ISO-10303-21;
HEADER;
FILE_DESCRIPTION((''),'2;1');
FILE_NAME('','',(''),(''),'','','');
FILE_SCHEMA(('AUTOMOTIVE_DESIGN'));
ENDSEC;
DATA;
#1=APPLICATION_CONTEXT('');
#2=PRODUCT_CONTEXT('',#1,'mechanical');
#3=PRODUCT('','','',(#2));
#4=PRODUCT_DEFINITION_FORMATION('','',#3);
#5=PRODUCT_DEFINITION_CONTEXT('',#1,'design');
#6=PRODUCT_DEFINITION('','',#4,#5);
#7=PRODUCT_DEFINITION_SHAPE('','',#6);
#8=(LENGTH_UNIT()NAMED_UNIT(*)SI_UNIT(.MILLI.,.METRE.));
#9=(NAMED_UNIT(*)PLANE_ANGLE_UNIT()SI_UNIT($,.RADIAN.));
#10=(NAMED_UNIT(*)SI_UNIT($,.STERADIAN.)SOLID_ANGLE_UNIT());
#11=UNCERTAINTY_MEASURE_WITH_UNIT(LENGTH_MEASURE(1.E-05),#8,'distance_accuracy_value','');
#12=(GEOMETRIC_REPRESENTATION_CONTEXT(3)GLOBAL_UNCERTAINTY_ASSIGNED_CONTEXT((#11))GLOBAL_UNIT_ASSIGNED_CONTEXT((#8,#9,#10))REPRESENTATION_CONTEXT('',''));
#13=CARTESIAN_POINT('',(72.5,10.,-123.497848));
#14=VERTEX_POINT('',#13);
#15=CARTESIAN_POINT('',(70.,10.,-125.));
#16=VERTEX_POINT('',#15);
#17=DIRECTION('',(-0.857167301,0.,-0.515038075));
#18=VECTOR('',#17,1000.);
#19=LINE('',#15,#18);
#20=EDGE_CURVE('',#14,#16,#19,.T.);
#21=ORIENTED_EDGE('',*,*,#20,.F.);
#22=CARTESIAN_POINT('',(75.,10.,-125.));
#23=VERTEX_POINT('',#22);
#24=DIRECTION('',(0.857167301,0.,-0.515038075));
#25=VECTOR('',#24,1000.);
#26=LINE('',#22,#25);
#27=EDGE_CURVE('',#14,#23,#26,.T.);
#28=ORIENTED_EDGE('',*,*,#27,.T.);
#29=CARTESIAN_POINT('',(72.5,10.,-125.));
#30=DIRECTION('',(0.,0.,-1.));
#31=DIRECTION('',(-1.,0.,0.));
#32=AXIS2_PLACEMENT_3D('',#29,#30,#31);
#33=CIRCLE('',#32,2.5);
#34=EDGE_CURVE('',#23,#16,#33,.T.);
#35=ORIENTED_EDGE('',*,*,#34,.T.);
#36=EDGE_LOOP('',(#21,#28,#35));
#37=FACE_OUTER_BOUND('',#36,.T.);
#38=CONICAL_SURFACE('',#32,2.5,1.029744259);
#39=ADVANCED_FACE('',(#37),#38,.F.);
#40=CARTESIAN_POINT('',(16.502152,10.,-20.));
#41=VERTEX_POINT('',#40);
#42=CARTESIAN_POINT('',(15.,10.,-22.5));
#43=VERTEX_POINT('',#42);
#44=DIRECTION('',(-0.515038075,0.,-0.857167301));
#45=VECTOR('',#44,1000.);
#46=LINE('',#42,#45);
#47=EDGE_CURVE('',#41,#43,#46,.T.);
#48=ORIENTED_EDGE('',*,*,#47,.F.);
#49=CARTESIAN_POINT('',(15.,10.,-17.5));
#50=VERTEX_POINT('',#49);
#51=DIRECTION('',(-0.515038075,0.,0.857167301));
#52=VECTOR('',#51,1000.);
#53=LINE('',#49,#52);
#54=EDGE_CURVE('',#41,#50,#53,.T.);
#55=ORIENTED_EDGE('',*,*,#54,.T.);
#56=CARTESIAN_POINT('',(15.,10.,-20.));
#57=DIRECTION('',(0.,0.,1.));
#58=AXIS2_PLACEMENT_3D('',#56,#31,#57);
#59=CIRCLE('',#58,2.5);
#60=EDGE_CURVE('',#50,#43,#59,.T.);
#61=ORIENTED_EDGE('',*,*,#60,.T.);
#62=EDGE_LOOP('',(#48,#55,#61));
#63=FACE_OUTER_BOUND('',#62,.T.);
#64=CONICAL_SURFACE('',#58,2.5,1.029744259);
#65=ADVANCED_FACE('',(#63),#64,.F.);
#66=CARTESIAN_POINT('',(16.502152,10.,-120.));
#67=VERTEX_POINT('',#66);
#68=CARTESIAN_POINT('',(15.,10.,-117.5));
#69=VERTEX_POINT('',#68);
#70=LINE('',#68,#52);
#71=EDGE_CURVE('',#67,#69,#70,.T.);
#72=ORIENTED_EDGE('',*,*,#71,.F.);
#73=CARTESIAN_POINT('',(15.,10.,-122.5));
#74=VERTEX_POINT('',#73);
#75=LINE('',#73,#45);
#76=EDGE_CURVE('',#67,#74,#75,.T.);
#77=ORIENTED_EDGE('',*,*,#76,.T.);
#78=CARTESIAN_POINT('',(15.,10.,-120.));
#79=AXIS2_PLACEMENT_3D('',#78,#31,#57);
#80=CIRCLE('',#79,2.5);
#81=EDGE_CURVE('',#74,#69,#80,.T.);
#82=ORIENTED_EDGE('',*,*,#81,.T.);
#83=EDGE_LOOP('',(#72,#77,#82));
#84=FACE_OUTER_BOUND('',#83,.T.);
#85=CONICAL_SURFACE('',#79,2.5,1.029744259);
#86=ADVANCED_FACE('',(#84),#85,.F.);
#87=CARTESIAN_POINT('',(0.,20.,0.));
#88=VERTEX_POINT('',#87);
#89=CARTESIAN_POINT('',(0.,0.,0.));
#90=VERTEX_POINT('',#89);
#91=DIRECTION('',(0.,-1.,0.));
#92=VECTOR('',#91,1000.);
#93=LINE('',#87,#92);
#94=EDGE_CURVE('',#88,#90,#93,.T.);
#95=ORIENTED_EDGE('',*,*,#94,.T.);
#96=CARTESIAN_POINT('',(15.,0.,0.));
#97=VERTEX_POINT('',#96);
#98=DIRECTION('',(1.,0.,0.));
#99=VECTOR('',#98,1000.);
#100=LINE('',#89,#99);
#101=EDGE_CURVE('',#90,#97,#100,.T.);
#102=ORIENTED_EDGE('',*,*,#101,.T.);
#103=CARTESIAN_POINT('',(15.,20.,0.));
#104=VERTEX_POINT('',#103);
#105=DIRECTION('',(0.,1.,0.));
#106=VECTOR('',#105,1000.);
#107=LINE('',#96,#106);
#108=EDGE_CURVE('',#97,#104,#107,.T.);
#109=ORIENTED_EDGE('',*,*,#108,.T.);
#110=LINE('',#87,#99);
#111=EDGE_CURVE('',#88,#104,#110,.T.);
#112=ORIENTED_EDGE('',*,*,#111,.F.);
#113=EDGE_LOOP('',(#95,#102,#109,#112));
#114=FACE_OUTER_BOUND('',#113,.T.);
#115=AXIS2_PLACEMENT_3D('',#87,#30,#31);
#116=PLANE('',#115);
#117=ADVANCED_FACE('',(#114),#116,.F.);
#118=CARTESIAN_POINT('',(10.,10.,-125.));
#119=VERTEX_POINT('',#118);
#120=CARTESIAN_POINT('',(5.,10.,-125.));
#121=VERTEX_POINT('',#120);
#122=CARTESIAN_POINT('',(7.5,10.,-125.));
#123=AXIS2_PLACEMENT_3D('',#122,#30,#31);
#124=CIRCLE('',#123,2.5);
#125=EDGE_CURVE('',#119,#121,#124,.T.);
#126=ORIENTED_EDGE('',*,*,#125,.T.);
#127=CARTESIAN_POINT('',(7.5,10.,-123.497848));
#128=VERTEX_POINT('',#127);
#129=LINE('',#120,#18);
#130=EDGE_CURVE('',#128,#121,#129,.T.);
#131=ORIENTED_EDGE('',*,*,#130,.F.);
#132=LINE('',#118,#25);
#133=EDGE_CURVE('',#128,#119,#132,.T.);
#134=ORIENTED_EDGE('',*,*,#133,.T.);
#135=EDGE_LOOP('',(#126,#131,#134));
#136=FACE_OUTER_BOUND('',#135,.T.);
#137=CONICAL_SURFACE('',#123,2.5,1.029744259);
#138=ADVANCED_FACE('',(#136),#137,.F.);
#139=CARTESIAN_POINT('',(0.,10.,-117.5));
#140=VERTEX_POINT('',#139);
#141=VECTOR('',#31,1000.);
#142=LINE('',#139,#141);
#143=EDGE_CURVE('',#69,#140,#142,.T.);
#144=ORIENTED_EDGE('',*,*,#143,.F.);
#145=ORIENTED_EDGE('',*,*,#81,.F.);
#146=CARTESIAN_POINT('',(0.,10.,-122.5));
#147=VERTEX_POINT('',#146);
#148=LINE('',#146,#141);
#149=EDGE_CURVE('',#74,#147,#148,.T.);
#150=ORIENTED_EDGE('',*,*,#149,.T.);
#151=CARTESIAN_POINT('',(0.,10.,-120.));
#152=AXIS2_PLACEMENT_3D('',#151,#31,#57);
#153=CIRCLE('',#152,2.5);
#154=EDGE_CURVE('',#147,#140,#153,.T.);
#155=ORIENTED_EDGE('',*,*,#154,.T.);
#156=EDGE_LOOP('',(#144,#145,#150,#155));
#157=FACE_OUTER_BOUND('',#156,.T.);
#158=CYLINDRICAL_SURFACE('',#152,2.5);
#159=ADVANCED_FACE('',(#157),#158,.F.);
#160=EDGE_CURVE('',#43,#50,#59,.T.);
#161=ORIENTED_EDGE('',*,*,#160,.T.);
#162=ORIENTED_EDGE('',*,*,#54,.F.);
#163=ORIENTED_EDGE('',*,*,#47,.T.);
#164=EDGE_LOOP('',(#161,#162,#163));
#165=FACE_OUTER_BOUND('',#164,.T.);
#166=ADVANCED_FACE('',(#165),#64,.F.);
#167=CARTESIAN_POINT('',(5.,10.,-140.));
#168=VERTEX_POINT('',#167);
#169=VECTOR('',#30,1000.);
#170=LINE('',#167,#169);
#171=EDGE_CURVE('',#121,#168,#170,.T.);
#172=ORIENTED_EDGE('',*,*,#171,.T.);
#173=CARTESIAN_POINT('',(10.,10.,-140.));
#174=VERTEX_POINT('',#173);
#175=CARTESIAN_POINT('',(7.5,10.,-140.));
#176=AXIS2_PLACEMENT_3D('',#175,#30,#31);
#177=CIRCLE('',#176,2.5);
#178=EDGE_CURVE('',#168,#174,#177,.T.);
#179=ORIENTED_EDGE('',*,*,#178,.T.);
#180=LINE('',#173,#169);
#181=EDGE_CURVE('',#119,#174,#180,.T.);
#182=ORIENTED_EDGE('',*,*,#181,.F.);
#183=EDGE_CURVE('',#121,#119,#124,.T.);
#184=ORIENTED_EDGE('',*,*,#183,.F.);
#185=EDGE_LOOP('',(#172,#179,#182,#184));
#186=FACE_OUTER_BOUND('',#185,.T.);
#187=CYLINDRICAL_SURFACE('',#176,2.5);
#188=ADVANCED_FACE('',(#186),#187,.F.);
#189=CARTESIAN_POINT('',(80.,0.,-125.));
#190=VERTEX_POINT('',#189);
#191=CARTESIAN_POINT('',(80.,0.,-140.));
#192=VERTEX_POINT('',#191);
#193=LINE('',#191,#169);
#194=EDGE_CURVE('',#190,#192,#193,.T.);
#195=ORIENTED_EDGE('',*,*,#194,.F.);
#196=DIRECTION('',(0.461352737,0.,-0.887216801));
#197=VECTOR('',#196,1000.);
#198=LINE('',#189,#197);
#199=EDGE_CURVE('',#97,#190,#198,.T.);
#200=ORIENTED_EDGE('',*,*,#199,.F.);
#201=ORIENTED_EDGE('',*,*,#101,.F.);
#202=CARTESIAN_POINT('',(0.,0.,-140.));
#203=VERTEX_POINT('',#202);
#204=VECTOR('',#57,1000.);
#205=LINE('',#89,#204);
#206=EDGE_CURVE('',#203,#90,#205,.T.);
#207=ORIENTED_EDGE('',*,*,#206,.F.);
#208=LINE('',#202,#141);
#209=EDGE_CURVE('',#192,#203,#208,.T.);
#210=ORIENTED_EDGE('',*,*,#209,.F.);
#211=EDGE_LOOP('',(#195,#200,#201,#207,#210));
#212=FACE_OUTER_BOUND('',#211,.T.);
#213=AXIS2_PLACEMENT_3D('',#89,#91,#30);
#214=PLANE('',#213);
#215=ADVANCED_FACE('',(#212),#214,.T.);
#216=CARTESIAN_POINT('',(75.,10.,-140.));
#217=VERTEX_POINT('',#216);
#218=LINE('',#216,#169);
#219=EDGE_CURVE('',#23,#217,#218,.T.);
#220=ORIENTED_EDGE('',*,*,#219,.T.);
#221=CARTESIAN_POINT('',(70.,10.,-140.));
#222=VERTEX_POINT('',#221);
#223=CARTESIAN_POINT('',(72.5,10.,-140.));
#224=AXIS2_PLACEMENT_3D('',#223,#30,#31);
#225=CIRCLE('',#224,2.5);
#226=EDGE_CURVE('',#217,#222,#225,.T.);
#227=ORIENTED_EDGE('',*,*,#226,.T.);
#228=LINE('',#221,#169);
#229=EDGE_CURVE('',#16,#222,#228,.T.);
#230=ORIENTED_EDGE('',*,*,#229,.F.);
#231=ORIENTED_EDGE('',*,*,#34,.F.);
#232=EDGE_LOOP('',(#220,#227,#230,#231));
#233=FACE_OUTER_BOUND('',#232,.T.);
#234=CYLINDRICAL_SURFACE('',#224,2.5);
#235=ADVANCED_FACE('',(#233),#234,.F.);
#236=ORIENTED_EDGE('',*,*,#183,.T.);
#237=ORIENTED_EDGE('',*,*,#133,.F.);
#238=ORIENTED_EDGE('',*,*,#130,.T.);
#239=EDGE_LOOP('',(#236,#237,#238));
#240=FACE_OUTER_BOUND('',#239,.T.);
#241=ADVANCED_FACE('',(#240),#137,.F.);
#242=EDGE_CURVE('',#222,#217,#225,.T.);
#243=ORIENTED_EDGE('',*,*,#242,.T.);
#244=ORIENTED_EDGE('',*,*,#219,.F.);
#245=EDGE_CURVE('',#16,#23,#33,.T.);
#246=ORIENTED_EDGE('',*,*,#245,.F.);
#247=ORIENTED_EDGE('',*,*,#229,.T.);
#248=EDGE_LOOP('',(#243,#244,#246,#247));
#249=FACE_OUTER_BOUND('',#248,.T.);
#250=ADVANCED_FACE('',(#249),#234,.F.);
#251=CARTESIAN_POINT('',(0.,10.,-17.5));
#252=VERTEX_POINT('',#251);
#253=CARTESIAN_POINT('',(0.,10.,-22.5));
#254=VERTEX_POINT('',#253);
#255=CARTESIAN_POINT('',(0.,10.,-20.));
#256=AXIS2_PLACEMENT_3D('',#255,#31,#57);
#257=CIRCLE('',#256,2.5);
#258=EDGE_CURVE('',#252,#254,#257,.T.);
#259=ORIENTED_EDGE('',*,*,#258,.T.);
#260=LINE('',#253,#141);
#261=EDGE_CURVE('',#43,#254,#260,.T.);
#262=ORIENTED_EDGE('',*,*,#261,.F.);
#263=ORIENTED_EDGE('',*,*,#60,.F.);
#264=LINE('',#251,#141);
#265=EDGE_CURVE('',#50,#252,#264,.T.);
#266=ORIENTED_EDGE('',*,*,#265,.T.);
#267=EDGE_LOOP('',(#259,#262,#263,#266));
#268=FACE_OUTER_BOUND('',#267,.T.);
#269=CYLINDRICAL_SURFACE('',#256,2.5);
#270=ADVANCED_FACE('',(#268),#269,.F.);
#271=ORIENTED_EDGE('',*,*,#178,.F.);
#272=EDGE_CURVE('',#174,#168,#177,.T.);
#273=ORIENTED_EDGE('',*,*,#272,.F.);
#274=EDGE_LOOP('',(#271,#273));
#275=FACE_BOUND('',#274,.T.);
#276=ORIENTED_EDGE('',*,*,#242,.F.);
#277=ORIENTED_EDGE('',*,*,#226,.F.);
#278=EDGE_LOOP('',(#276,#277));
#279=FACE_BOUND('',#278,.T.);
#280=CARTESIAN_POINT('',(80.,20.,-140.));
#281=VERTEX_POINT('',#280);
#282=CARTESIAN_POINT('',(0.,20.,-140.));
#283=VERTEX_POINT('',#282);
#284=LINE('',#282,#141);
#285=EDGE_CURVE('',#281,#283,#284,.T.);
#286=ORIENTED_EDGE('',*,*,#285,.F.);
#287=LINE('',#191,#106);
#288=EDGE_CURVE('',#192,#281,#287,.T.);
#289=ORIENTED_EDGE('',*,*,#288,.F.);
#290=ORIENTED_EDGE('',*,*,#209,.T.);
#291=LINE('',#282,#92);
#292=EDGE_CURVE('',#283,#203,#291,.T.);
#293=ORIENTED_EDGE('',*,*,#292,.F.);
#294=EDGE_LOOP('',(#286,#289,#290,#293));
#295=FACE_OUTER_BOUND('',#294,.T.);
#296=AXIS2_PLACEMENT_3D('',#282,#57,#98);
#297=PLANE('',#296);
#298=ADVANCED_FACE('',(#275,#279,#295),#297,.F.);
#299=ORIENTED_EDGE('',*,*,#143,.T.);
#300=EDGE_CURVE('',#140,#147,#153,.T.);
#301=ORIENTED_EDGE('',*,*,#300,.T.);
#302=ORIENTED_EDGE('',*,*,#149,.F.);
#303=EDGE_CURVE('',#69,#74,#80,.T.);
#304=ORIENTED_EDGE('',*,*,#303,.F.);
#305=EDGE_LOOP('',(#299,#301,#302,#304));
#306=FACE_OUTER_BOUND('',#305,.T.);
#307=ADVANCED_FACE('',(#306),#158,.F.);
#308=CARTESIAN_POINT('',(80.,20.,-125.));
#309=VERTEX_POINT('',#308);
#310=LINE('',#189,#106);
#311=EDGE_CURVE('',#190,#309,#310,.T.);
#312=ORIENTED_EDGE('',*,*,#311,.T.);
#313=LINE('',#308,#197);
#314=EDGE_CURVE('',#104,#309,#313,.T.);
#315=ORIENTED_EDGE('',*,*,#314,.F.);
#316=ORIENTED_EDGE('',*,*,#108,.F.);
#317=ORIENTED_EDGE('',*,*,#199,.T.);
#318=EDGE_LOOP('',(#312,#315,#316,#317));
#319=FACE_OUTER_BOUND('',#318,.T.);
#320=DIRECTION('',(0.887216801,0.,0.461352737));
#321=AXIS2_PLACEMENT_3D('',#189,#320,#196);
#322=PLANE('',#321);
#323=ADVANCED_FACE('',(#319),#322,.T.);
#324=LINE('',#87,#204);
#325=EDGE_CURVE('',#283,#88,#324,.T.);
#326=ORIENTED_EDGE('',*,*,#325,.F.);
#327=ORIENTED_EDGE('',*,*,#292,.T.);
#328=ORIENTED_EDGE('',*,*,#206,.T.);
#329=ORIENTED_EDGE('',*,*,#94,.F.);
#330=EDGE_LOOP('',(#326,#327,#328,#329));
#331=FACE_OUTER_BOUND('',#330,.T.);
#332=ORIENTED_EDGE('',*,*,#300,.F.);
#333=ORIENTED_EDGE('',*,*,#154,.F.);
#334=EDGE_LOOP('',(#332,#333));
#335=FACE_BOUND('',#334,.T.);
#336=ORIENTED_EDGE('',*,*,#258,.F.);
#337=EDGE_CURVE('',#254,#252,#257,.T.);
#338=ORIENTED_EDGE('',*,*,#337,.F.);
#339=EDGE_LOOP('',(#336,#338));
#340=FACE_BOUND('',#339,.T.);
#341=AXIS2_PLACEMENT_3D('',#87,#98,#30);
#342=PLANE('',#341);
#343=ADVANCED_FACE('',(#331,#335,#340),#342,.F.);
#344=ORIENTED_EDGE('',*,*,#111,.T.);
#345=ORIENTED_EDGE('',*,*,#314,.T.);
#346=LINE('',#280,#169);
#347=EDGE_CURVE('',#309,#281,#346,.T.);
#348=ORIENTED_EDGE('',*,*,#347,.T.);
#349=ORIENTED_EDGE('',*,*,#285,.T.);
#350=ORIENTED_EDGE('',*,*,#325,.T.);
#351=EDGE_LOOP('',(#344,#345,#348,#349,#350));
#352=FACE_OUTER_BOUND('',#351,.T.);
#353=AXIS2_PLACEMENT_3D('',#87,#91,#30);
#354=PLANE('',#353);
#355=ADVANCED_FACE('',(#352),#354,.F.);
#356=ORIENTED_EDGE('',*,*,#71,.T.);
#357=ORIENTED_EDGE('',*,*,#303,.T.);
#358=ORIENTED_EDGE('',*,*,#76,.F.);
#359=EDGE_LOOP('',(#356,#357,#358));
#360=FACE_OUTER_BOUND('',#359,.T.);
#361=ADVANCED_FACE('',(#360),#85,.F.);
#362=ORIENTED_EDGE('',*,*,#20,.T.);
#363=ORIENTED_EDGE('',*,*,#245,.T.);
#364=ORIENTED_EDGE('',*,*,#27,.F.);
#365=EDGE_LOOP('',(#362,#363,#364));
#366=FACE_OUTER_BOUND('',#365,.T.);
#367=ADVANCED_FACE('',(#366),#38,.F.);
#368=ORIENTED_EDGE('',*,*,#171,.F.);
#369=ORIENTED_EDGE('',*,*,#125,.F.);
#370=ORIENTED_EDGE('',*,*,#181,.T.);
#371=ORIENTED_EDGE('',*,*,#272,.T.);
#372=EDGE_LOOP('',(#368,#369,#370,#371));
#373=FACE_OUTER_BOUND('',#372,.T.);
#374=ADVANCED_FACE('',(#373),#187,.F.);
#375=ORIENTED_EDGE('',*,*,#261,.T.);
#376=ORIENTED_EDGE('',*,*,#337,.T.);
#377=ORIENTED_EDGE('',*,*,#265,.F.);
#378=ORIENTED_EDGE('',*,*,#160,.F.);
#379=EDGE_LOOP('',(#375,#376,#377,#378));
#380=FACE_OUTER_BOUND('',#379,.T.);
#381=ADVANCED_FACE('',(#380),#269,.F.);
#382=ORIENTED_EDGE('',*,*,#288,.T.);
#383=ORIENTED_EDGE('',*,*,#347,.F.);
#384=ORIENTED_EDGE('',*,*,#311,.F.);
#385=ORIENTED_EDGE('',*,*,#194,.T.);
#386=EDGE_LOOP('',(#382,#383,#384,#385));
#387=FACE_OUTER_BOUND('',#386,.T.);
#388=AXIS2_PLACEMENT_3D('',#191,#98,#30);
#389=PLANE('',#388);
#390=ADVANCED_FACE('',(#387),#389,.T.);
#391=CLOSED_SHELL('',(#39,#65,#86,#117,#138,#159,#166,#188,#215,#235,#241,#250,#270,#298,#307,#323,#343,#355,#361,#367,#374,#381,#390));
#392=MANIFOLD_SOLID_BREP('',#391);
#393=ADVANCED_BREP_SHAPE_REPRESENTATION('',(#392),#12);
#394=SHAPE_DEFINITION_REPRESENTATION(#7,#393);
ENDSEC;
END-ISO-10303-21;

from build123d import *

# Parameters (mm, degrees)
SKETCH_1_W             = 200
SKETCH_1_H             = 140
EXTRUDE_1_DEPTH        = 20
SKETCH_3_OUTSIDE_W     = 250.99
SKETCH_3_OUTSIDE_H     = 190.99
CUT_EXTRUDE_1_DEPTH    = 245.948974278
HOLE_WIZARD_M6_1_D     = 5
HOLE_WIZARD_M6_1_DEPTH = 15
HOLE_WIZARD_M6_1_TIP   = 1.502151548
HOLE_WIZARD_M6_2_D     = 5
HOLE_WIZARD_M6_2_DEPTH = 15
HOLE_WIZARD_M6_2_TIP   = 1.502151548


with BuildPart() as part:
    # 草图1 → 凸台-拉伸1 (new body)
    with BuildSketch(Plane(origin=(0, 0, 0), x_dir=(1, 0, 0), z_dir=(0, 1, 0))):
        with Locations((100, 70)):
            Rectangle(SKETCH_1_W, SKETCH_1_H)
    extrude(amount=EXTRUDE_1_DEPTH)

    # 草图3 outside → 切除-拉伸1 (cut, through all)
    with BuildSketch(Plane(origin=(0, 20, 0), x_dir=(1, 0, 0), z_dir=(0, 1, 0))):
        with Locations((100, 70)):
            Rectangle(SKETCH_3_OUTSIDE_W, SKETCH_3_OUTSIDE_H)
        Polygon((0, 140), (80, 140), (80, 125), (15, 0), (0, 0), align=None, mode=Mode.SUBTRACT)
    extrude(amount=-CUT_EXTRUDE_1_DEPTH, mode=Mode.SUBTRACT)

    # M6 螺纹孔1
    with Locations(Plane.ZY):
        with Locations((-120, 10), (-20, 10)):
            Hole(HOLE_WIZARD_M6_1_D / 2, depth=HOLE_WIZARD_M6_1_DEPTH)
            with Locations((0, 0, -(HOLE_WIZARD_M6_1_DEPTH + HOLE_WIZARD_M6_1_TIP / 2))):  # 118° drill point
                Cone(0, HOLE_WIZARD_M6_1_D / 2, HOLE_WIZARD_M6_1_TIP, mode=Mode.SUBTRACT)

    # M6 螺纹孔2
    with Locations(Plane(origin=(0, 0, -140), x_dir=(-1, 0, 0), z_dir=(0, 0, -1))):
        with Locations((-72.5, 10), (-7.5, 10)):
            Hole(HOLE_WIZARD_M6_2_D / 2, depth=HOLE_WIZARD_M6_2_DEPTH)
            with Locations((0, 0, -(HOLE_WIZARD_M6_2_DEPTH + HOLE_WIZARD_M6_2_TIP / 2))):  # 118° drill point
                Cone(0, HOLE_WIZARD_M6_2_D / 2, HOLE_WIZARD_M6_2_TIP, mode=Mode.SUBTRACT)


solid = part.part
